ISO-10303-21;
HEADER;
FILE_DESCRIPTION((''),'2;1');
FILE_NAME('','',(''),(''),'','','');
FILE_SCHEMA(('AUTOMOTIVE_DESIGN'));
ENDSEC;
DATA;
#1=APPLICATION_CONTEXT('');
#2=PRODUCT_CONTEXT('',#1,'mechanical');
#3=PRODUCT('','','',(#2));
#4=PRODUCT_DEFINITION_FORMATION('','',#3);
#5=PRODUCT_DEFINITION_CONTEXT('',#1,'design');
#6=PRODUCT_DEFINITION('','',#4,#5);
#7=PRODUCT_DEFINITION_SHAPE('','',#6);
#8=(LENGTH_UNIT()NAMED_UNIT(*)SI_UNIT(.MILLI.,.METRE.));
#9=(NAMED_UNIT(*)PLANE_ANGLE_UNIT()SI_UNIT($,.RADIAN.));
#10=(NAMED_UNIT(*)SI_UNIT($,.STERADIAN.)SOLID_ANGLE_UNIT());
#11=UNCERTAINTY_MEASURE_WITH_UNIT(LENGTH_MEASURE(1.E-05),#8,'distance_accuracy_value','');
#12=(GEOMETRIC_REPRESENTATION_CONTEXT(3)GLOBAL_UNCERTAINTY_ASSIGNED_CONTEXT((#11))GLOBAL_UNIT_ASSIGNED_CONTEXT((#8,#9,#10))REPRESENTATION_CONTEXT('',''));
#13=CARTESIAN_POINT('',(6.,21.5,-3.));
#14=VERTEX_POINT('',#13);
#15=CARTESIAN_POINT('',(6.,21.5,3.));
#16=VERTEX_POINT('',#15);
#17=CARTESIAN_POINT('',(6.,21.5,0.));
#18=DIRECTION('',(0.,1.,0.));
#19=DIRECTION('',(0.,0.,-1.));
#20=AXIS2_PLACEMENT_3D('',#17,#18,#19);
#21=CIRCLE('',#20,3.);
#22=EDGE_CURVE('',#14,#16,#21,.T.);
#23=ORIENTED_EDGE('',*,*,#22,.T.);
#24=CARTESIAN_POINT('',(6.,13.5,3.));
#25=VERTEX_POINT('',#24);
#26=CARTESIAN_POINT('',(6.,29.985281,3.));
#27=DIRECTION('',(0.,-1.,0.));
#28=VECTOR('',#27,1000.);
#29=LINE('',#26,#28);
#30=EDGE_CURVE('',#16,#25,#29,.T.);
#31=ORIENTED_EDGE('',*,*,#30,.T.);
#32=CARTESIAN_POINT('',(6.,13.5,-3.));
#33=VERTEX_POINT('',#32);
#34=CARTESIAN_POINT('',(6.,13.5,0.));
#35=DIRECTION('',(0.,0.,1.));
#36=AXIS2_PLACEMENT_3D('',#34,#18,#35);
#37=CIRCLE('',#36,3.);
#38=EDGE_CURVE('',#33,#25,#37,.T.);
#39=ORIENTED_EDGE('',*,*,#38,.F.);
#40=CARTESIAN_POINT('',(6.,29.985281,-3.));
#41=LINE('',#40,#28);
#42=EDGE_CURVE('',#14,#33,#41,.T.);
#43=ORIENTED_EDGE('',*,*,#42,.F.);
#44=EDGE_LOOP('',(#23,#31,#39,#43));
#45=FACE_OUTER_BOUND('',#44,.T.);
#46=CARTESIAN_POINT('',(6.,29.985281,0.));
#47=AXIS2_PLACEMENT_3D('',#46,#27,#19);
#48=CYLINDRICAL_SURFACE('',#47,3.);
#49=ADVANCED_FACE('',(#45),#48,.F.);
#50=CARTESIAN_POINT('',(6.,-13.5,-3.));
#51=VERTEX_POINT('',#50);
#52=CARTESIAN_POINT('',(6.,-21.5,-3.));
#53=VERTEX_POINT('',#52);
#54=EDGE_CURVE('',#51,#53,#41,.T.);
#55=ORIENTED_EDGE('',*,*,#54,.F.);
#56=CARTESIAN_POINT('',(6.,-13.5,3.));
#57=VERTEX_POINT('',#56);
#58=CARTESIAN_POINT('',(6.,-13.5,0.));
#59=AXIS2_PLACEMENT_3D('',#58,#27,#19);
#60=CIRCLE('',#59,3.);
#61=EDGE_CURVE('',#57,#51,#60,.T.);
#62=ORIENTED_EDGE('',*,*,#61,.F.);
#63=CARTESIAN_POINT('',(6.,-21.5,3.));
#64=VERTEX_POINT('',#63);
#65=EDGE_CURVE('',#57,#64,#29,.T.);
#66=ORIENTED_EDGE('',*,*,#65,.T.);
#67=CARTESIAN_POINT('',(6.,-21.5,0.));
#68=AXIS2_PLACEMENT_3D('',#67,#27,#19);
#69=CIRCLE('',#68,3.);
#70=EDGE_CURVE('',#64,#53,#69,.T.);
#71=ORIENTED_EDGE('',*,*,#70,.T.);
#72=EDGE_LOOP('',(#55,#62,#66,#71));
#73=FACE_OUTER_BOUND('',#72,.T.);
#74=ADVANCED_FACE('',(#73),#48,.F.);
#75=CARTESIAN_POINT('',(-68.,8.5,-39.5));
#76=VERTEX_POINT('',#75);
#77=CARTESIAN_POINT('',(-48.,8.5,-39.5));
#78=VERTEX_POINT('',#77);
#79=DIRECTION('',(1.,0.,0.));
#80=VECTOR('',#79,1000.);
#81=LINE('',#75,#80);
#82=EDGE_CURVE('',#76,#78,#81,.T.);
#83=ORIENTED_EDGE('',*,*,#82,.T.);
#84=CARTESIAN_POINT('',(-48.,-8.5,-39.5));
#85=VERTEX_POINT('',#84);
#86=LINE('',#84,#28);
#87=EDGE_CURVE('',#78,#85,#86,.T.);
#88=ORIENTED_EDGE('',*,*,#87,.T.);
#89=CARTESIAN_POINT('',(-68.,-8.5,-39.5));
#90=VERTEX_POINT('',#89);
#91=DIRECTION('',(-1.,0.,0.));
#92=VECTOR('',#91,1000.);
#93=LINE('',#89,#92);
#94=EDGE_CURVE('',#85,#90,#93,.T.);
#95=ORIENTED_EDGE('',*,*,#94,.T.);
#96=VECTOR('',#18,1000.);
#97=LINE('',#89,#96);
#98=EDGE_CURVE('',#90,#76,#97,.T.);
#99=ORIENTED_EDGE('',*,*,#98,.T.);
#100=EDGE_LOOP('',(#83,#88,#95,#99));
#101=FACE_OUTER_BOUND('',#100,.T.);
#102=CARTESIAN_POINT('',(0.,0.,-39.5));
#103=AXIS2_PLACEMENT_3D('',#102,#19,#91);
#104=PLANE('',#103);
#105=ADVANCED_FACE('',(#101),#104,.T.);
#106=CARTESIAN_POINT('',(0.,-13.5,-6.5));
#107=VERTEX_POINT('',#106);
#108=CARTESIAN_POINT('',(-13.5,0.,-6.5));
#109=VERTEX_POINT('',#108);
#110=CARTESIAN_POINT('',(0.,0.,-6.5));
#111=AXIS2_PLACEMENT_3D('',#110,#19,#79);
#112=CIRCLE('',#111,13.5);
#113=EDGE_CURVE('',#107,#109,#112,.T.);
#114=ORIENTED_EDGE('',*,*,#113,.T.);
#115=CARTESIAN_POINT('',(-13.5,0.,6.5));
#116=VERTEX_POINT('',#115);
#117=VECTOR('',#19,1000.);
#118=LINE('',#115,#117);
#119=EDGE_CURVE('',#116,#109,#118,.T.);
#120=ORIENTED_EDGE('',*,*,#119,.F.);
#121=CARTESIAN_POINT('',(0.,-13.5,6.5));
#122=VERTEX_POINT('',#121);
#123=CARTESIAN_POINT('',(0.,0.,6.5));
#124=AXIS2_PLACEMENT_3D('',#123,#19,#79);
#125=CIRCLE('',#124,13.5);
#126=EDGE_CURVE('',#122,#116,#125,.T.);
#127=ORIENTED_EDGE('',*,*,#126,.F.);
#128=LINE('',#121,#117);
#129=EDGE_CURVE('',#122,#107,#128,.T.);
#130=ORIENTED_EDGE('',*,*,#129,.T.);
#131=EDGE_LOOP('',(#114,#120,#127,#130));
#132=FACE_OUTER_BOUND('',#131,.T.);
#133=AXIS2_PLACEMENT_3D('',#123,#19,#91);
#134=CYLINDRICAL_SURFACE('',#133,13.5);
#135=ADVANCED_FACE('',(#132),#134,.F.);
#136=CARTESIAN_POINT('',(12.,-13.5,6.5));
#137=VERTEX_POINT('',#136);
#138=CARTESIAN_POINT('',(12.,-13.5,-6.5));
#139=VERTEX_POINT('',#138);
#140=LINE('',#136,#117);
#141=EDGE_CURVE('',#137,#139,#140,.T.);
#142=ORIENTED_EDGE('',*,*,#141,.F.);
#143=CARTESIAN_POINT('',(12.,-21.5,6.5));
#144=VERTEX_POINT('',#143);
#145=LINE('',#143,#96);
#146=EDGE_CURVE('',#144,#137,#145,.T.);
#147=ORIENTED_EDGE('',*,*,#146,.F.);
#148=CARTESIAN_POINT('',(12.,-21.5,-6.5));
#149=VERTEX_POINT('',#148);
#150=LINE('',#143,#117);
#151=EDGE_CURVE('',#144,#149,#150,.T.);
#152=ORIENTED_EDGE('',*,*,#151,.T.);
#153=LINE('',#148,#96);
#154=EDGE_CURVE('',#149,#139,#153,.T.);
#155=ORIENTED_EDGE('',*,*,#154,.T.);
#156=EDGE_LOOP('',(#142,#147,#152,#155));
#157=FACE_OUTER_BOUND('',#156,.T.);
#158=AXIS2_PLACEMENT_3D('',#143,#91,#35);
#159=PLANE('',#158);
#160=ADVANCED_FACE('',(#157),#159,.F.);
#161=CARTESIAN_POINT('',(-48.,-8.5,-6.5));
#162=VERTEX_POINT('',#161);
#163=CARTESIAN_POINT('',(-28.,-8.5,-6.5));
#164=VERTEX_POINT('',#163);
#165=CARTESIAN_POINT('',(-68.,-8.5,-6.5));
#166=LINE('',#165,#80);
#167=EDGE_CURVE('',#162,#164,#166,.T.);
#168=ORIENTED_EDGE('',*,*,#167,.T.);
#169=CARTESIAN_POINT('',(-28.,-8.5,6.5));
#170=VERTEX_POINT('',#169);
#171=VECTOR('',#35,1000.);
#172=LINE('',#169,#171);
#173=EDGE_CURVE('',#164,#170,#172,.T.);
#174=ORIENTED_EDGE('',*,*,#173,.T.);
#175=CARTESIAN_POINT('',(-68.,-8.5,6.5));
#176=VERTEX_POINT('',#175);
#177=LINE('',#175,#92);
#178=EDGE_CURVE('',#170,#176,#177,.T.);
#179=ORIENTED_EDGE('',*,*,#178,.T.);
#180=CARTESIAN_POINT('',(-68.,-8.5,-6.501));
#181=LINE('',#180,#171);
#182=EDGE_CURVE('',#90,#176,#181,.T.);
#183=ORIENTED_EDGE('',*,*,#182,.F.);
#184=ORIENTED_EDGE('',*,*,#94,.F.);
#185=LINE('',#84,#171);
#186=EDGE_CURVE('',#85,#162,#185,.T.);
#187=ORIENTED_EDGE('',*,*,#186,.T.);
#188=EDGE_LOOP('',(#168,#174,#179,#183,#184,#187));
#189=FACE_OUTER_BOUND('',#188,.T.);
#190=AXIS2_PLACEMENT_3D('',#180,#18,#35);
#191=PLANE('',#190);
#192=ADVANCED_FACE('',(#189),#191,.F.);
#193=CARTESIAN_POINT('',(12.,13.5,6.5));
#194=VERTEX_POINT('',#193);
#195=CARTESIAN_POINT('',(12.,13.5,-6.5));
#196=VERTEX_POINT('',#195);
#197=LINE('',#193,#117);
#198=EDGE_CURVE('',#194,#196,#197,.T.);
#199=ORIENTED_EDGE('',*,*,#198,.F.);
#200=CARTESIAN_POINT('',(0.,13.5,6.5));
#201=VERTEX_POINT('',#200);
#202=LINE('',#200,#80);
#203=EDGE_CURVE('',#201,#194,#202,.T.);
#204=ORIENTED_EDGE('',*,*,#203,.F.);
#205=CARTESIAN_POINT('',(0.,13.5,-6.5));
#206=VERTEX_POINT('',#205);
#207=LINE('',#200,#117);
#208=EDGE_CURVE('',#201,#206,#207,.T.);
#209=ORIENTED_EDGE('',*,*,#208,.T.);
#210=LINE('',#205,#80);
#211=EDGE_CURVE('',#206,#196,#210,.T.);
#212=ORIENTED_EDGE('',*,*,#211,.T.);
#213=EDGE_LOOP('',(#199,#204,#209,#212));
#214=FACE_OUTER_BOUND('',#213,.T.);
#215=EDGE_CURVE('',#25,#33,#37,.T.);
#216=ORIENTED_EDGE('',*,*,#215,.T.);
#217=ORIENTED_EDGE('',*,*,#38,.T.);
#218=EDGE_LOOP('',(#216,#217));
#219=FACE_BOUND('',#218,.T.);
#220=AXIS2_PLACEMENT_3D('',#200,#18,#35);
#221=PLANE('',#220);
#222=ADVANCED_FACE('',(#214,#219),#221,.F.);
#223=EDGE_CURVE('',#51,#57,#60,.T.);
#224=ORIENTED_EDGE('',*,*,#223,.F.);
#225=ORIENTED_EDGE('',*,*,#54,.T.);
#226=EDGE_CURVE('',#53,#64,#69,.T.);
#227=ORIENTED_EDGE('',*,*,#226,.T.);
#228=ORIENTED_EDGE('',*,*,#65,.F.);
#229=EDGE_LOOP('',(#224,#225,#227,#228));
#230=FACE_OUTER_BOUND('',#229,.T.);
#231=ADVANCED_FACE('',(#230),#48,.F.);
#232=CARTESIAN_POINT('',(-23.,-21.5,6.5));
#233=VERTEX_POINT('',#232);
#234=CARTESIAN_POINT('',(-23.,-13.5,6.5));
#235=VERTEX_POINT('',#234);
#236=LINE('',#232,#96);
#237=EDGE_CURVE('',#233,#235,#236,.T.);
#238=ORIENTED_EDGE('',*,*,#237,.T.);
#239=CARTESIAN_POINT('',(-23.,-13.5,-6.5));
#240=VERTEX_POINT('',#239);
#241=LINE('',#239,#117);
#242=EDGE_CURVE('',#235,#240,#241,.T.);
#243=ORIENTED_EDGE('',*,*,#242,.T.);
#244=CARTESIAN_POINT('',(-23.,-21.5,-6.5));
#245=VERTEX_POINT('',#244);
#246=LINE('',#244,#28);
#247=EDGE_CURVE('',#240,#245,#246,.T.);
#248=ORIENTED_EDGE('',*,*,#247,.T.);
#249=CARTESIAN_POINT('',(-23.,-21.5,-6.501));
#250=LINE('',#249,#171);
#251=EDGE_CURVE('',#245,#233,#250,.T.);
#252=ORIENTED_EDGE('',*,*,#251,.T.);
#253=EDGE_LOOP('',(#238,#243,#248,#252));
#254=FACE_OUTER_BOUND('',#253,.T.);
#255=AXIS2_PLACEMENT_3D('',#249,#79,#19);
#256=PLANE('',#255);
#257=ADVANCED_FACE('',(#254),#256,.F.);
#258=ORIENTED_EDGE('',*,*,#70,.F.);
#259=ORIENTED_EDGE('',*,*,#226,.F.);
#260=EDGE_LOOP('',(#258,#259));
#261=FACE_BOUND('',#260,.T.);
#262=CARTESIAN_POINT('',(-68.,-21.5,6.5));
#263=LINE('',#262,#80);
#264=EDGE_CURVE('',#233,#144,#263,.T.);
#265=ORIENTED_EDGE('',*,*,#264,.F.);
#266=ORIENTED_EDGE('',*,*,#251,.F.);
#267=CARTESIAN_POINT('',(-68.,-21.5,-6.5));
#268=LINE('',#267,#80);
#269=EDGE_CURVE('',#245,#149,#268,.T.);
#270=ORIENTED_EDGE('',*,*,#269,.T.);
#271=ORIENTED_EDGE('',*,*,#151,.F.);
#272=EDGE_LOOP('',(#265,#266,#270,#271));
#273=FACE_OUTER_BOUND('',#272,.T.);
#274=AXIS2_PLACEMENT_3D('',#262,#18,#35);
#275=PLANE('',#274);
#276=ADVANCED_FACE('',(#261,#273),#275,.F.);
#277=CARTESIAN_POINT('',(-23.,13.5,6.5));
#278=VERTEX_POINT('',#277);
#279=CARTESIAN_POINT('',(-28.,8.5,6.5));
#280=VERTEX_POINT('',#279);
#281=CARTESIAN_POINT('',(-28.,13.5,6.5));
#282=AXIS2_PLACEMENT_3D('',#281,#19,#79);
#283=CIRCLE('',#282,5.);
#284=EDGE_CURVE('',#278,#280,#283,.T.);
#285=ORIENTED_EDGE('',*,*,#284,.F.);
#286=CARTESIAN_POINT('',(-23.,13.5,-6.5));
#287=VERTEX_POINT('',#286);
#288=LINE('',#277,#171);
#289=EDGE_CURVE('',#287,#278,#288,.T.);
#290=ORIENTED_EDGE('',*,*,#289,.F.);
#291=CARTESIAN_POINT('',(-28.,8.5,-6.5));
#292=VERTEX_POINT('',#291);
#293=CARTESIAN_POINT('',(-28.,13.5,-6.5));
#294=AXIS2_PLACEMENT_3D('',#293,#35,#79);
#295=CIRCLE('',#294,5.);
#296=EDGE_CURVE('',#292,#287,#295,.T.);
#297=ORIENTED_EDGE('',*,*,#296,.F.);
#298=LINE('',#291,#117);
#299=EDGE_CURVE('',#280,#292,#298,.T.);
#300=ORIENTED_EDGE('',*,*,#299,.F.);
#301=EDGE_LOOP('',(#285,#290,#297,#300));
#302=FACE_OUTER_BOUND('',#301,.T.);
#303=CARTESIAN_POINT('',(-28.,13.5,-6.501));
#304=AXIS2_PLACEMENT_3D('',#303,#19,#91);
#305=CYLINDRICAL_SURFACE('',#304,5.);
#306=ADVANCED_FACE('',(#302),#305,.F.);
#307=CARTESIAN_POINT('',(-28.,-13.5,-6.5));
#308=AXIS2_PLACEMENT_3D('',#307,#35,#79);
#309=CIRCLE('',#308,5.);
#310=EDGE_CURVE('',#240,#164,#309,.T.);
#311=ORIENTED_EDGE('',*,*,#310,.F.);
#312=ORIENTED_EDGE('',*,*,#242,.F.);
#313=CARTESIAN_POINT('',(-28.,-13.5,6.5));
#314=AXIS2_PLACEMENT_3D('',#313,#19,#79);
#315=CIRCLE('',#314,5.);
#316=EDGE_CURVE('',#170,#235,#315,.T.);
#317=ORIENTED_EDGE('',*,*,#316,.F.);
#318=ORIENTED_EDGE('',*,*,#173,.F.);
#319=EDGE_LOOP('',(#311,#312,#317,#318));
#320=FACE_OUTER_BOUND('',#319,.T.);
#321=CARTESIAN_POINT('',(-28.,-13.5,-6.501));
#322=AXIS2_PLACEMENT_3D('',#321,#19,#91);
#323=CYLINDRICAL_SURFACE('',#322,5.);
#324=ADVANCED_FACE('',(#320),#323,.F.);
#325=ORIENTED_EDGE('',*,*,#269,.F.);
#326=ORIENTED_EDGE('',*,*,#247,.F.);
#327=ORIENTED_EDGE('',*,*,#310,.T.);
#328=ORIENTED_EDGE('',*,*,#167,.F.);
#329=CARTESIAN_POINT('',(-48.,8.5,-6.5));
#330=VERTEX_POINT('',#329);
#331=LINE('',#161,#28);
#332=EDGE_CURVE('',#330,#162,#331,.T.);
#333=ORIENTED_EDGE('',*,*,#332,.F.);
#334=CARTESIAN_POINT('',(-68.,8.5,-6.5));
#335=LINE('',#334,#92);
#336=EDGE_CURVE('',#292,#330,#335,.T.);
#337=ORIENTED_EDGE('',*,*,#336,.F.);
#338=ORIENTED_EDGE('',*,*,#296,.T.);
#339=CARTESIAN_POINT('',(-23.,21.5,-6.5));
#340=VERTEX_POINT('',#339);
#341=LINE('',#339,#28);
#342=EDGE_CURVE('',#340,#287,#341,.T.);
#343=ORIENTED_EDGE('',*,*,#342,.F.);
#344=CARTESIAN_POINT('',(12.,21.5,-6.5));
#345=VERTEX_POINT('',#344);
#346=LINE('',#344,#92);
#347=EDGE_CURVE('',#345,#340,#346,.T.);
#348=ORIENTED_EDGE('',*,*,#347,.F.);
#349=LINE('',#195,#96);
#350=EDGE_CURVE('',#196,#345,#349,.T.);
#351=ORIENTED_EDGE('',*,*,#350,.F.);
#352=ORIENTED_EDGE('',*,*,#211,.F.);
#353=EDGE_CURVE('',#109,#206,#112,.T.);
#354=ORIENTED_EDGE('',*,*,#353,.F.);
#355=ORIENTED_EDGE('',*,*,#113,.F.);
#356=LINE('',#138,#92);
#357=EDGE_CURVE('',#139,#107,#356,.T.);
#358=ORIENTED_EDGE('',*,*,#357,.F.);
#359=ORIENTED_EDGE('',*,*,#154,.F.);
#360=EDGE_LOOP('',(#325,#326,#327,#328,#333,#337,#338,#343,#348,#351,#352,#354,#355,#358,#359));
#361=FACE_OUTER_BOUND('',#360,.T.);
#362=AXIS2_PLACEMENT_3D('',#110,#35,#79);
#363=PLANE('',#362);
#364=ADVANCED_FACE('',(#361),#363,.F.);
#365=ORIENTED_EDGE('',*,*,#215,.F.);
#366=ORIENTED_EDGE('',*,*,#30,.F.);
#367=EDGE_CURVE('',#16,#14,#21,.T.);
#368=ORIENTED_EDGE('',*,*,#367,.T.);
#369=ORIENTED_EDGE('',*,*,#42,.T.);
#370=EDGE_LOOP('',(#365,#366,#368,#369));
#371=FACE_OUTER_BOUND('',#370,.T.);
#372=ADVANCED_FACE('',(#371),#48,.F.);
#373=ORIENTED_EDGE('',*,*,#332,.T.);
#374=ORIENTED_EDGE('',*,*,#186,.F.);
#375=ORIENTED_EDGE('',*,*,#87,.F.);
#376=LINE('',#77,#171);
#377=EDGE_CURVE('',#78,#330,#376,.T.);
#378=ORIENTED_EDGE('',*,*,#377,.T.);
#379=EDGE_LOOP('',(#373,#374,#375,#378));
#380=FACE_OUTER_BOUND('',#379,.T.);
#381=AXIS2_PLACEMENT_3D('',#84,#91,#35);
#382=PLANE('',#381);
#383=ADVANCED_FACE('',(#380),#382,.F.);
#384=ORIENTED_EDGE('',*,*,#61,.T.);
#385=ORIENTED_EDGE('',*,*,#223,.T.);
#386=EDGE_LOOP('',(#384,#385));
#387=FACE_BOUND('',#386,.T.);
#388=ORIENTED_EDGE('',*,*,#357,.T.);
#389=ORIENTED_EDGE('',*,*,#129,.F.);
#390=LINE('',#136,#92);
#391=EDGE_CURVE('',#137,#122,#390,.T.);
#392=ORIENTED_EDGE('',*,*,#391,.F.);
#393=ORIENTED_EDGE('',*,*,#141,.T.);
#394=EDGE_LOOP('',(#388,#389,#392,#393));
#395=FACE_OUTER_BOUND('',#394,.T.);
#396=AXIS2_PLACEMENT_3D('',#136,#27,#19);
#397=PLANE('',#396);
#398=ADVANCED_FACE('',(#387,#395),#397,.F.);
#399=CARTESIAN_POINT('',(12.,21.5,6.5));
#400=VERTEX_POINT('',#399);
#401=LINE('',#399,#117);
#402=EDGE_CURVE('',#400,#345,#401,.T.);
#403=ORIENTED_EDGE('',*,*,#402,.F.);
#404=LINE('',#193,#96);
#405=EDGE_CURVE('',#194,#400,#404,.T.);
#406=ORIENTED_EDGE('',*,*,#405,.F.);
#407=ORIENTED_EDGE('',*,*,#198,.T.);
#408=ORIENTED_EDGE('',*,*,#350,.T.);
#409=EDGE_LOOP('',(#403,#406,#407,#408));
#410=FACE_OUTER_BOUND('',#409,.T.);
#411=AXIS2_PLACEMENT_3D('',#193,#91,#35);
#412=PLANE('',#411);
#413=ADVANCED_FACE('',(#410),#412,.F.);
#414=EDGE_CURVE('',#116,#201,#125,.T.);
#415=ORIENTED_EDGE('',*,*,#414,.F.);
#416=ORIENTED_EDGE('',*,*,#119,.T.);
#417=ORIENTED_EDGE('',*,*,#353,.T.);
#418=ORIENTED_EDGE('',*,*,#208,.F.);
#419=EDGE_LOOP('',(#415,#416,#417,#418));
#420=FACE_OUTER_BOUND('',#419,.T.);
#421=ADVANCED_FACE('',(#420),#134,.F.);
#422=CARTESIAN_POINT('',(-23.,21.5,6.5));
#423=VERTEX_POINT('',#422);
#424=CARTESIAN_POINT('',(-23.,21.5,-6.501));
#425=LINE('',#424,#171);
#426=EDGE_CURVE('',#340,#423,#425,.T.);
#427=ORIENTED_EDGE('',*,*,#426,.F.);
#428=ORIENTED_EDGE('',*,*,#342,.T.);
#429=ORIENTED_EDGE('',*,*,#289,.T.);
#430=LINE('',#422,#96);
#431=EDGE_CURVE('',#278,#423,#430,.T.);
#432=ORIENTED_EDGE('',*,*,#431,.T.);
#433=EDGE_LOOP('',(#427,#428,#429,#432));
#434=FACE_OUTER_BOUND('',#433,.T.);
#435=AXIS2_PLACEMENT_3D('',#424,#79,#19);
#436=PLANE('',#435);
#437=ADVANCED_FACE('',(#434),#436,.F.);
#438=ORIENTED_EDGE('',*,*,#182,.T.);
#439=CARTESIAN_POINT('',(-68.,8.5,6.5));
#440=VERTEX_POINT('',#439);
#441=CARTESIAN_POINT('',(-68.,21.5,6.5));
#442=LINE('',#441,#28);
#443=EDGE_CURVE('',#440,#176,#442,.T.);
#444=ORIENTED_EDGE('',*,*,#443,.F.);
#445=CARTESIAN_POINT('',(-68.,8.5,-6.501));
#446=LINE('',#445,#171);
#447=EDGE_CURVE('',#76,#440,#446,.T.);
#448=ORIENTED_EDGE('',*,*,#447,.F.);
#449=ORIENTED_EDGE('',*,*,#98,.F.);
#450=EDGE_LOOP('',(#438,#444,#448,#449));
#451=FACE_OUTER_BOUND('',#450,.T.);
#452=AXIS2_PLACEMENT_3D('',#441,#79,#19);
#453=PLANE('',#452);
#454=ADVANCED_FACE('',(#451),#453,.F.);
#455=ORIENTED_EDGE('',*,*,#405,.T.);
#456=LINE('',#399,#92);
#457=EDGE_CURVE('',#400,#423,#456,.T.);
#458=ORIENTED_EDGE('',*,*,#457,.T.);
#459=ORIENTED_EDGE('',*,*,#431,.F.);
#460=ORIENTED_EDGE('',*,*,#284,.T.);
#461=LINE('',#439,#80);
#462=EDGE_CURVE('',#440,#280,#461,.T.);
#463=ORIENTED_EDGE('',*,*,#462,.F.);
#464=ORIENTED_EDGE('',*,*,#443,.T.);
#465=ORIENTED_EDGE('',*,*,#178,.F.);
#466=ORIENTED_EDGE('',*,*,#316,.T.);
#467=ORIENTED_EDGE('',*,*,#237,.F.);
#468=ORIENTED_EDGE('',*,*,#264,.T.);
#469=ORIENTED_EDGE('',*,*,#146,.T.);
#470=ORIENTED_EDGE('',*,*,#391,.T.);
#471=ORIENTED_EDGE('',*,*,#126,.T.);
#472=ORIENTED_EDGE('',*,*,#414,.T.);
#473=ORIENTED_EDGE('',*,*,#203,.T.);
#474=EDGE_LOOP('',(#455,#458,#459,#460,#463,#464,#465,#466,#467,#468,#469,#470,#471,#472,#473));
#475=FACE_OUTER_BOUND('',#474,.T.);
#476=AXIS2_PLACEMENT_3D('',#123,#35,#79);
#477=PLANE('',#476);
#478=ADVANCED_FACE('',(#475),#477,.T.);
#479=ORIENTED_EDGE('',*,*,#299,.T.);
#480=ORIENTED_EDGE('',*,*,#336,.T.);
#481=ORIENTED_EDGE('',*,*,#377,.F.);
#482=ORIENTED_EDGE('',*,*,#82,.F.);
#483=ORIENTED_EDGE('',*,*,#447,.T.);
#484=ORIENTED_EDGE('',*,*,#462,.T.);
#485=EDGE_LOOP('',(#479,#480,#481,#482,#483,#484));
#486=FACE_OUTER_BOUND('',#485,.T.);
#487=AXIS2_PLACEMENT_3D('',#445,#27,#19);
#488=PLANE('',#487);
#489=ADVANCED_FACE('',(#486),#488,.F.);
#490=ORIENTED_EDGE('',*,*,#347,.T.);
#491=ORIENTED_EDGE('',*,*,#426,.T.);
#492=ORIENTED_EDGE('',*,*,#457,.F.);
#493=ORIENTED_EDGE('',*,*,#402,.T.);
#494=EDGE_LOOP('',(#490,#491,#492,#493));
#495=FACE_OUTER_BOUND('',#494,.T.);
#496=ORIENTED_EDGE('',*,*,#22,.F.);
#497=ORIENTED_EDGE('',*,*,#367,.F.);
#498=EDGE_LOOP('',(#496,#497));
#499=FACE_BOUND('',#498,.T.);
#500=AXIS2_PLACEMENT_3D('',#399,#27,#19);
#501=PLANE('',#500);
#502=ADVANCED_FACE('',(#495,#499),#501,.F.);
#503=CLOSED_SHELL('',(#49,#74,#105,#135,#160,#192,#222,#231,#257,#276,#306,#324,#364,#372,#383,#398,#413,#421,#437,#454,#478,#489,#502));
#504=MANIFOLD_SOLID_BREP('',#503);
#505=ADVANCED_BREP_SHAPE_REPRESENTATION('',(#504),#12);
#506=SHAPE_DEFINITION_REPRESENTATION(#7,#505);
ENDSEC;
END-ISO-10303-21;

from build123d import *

# Parameters (mm, degrees)
EXTRUDE_1_DEPTH     = 6.5
CUT_EXTRUDE_1_REACH = 74.493
SKETCH_2_W          = 45
SKETCH_2_H          = 13
FILLET_1_R          = 5
SKETCH_3_W          = 20
SKETCH_3_H          = 17
EXTRUDE_2_DEPTH     = 33
CUT_EXTRUDE_2_REACH = 91.628
SKETCH_4_R          = 3


with BuildPart() as part:
    # 草图1 → 凸台-拉伸1 (new, symmetric)
    with BuildSketch(Plane.XY):
        with BuildLine():
            Line((0, 13.5), (12, 13.5))
            Line((12, 13.5), (12, 21.5))
            Line((12, 21.5), (-68, 21.5))
            Line((-68, 21.5), (-68, -21.5))
            Line((-68, -21.5), (12, -21.5))
            Line((12, -21.5), (12, -13.5))
            Line((12, -13.5), (0, -13.5))
            ThreePointArc((0, -13.5), (-13.5, 0), (0, 13.5))
        make_face()
    extrude(amount=EXTRUDE_1_DEPTH, both=True)

    # 草图2 → 切除-拉伸1 (cut, up to next)
    with BuildSketch(Plane.XY.offset(6.5), mode=Mode.PRIVATE) as cut_extrude_1_sk1:
        with Locations((-45.5, 15)):
            Rectangle(SKETCH_2_W, SKETCH_2_H)
    cut_extrude_1_tool1 = extrude(cut_extrude_1_sk1.sketch, amount=-CUT_EXTRUDE_1_REACH, mode=Mode.PRIVATE) & part.part
    # 草图2 → 切除-拉伸1 (cut, up to next)
    with BuildSketch(Plane.XY.offset(6.5), mode=Mode.PRIVATE) as cut_extrude_1_sk2:
        with Locations((-45.5, -15)):
            Rectangle(SKETCH_2_W, SKETCH_2_H)
    cut_extrude_1_tool2 = extrude(cut_extrude_1_sk2.sketch, amount=-CUT_EXTRUDE_1_REACH, mode=Mode.PRIVATE) & part.part
    add(cut_extrude_1_tool1.solids().sort_by_distance((-45.5, 15, 6.5))[0], mode=Mode.SUBTRACT)
    add(cut_extrude_1_tool2.solids().sort_by_distance((-45.5, -15, 6.5))[0], mode=Mode.SUBTRACT)

    # 圆角1
    fillet_1_edges = [part.edges().sort_by_distance(p)[0] for p in [
        (-23, 8.5, 0),
        (-23, -8.5, 0),
    ]]
    fillet(fillet_1_edges, radius=FILLET_1_R)

    # 草图3 → 凸台-拉伸2 (add)
    with BuildSketch(Plane(origin=(0, 0, -6.5), x_dir=(-1, 0, 0), z_dir=(0, 0, -1))):
        with Locations((58, 0)):
            Rectangle(SKETCH_3_W, SKETCH_3_H)
    extrude(amount=EXTRUDE_2_DEPTH)

    # 切除-拉伸2: up to this face of the body (flat: up to its plane)
    cut_extrude_2_end = Plane(part.part.faces().sort_by_distance((-5.5, 21.5, 0))[0])
    # 草图4 → 切除-拉伸2 (cut, up to the picked face)
    with BuildSketch(Plane.XZ.offset(21.5), mode=Mode.PRIVATE) as cut_extrude_2_sk1:
        with Locations(Location((6, 0, 0), (0, 0, 270))):
            Circle(SKETCH_4_R)
    cut_extrude_2_tool1 = split(extrude(cut_extrude_2_sk1.sketch, amount=-CUT_EXTRUDE_2_REACH, mode=Mode.PRIVATE), bisect_by=cut_extrude_2_end, keep=Keep.BOTH, mode=Mode.PRIVATE)
    add(cut_extrude_2_tool1.solids().sort_by(Axis((6, -21.5, 0), (0, 1, 0)))[0], mode=Mode.SUBTRACT)


solid = part.part
